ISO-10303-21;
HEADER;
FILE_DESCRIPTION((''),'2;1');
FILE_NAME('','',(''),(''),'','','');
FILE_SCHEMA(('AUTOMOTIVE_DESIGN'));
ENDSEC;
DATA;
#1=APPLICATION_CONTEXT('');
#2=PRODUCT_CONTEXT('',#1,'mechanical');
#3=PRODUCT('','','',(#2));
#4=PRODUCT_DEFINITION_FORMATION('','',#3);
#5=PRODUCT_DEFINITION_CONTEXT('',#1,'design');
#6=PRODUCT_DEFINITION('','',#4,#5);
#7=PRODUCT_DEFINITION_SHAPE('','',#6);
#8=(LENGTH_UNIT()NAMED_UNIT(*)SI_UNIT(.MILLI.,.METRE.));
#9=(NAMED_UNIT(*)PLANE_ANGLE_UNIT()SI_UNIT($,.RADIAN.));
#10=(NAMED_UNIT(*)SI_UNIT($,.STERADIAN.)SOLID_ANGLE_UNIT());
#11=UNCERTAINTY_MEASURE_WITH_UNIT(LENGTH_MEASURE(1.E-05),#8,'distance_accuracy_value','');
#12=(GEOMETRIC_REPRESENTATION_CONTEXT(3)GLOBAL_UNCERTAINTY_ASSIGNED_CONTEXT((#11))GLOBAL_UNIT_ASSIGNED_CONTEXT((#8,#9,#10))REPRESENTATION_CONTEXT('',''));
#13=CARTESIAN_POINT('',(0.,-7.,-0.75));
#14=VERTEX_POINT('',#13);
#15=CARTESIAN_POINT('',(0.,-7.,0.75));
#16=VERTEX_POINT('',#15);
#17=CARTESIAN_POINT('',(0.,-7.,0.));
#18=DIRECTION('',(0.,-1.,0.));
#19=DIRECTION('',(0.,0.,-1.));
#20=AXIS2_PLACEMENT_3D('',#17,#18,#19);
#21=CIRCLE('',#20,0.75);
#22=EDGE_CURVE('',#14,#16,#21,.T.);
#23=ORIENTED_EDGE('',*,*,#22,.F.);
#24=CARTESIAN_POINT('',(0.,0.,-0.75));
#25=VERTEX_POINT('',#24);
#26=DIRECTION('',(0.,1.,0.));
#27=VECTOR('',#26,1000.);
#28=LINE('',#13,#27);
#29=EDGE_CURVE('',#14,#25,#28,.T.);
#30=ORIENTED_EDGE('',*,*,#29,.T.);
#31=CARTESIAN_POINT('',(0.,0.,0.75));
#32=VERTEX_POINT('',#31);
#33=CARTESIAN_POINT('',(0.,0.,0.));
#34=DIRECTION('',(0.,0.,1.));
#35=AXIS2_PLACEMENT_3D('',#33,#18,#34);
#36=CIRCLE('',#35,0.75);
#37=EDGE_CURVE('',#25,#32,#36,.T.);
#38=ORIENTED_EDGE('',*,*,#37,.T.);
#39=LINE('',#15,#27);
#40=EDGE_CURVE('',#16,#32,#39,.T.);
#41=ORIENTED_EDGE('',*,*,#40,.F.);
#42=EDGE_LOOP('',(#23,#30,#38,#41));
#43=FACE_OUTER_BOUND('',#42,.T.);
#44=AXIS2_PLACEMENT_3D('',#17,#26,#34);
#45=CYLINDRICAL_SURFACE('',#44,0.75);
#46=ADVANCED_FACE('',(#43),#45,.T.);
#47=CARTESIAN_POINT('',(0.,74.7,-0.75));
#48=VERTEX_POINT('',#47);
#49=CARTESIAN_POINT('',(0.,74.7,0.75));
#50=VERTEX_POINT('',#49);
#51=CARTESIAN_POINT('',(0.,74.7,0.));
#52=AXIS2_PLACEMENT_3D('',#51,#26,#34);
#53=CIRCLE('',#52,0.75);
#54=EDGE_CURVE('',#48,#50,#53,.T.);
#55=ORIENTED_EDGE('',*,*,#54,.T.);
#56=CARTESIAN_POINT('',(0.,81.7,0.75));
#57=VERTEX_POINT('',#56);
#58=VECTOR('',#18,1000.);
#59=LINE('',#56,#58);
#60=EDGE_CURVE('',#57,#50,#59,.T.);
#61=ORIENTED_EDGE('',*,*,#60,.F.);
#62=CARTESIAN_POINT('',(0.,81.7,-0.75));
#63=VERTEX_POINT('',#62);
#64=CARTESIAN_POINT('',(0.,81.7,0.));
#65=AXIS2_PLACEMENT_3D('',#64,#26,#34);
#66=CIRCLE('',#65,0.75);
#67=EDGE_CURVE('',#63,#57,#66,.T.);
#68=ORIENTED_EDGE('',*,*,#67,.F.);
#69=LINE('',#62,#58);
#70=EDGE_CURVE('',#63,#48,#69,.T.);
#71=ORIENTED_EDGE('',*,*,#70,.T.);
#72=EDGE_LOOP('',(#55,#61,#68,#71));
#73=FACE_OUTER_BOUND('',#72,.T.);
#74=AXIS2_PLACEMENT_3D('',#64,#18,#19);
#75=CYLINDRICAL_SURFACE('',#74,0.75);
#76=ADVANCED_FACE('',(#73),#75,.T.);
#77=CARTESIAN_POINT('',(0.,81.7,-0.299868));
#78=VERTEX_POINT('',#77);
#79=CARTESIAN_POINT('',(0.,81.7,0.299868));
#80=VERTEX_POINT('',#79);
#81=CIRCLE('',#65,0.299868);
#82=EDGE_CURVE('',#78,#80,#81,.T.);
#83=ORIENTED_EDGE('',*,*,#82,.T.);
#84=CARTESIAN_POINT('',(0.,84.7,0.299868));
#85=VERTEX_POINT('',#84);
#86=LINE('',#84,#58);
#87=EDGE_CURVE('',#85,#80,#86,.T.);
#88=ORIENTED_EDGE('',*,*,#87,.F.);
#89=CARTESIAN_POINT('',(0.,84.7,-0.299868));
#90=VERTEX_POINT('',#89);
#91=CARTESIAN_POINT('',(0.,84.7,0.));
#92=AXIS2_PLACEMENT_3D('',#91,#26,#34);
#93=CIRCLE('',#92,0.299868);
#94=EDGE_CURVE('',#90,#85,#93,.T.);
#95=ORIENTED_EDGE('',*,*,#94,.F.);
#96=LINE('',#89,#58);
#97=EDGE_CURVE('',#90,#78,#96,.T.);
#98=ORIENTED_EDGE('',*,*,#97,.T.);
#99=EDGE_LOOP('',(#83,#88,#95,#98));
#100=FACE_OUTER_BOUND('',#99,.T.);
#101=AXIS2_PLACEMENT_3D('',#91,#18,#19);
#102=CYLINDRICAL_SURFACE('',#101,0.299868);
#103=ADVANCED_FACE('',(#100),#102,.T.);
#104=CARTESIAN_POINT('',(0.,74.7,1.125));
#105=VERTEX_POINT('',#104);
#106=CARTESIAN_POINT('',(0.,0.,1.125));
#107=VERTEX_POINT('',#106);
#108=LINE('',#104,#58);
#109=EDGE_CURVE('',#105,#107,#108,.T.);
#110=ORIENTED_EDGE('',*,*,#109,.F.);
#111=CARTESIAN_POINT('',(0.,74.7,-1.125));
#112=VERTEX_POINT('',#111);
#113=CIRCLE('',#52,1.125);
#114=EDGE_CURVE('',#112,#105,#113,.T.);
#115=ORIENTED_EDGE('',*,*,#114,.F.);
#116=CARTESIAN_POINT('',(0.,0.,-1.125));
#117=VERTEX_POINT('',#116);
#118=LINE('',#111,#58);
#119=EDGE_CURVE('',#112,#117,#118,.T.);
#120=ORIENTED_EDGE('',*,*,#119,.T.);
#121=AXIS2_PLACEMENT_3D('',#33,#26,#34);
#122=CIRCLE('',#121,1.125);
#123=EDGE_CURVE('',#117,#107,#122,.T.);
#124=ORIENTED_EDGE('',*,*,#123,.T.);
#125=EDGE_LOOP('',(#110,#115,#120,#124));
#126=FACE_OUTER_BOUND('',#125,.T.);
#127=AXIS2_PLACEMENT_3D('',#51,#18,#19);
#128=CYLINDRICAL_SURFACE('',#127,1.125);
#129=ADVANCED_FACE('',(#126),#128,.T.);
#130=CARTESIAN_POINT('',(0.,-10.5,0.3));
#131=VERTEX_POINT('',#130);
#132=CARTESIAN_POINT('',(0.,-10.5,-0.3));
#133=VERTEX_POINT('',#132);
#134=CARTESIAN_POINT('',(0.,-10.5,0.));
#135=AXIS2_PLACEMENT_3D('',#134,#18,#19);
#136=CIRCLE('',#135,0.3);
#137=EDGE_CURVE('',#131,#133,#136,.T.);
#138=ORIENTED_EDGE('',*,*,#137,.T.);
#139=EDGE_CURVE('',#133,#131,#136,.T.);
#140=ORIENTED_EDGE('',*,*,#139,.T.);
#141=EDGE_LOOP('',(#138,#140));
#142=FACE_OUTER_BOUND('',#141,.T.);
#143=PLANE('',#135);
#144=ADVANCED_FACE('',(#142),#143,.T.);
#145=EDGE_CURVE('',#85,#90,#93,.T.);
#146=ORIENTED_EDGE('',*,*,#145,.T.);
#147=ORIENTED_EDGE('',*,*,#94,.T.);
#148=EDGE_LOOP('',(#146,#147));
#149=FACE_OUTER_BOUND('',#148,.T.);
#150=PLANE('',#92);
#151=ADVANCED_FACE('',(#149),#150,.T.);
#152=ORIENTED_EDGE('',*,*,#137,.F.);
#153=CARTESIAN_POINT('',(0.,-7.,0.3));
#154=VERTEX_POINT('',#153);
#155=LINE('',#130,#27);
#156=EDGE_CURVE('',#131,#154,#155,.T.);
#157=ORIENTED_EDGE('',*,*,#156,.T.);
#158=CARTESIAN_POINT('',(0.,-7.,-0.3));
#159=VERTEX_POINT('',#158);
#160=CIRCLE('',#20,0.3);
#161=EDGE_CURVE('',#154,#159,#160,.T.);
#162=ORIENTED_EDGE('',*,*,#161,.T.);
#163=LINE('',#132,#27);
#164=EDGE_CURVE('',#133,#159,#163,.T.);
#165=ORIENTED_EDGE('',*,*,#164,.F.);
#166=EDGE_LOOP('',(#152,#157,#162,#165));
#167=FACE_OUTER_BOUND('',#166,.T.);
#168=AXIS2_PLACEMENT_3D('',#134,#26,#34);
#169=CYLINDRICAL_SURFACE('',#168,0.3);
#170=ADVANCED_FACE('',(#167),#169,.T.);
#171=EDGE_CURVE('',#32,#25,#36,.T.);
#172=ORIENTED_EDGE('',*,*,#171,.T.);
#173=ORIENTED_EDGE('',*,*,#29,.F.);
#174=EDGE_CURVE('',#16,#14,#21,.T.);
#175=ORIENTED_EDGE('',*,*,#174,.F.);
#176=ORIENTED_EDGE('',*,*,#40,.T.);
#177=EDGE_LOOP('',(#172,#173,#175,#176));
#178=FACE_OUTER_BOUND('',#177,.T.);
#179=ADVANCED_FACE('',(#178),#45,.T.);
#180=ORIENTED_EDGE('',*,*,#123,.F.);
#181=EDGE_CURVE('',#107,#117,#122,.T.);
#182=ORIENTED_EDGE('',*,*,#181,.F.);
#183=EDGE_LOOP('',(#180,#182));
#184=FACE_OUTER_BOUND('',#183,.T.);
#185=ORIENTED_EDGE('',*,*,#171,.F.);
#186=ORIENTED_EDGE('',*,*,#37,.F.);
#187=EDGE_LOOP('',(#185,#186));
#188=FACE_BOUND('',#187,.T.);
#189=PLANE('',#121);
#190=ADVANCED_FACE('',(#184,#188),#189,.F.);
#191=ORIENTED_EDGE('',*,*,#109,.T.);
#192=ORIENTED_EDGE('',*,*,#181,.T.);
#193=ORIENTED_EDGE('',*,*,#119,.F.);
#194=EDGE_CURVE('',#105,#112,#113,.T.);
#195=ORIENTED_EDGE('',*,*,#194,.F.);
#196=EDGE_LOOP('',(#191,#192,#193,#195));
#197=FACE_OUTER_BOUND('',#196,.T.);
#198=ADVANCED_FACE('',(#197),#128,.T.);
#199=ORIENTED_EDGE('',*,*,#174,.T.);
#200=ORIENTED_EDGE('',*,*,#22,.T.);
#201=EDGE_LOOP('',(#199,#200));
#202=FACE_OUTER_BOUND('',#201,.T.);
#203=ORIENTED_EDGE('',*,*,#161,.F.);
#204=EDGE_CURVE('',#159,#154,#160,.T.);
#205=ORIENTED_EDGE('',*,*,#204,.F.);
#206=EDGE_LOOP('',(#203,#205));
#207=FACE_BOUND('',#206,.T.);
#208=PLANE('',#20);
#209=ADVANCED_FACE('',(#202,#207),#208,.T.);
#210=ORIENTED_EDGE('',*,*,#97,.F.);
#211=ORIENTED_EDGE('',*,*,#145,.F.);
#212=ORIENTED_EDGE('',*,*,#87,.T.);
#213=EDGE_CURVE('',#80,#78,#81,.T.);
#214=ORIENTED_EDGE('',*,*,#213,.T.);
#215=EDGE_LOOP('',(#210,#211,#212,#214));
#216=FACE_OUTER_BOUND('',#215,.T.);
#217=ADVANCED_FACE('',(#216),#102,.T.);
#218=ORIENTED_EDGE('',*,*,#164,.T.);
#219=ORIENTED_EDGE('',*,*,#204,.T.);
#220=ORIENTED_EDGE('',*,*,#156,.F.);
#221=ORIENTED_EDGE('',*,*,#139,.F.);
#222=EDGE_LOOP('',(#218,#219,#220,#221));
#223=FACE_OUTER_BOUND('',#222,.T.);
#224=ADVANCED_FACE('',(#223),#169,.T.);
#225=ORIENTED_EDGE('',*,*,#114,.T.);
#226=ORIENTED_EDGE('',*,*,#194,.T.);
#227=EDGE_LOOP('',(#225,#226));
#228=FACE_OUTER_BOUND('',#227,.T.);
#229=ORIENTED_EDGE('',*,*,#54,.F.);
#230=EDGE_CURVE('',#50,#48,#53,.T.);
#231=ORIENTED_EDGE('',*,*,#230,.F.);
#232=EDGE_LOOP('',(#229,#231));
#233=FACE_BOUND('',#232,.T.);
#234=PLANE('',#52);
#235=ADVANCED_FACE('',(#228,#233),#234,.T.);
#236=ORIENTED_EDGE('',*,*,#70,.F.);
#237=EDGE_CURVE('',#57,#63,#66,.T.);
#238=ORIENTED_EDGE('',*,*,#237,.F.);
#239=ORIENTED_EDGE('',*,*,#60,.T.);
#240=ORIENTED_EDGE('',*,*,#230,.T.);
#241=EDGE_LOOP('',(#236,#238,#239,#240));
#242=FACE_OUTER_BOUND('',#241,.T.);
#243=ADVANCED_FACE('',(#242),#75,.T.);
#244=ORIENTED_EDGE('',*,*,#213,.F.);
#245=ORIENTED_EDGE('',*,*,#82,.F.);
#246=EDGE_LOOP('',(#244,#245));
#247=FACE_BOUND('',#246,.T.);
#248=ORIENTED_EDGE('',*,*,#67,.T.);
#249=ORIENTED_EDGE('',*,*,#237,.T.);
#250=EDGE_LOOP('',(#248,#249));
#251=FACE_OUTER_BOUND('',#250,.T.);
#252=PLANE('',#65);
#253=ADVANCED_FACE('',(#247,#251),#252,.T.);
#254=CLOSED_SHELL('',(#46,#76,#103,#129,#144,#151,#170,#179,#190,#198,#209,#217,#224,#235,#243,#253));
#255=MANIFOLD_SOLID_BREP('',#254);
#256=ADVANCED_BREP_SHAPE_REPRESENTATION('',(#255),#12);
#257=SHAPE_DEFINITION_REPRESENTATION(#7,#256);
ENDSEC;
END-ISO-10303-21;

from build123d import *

# Parameters (mm, degrees)
SKETCH1_R           = 1.125
BOSS_EXTRUDE1_DEPTH = 74.7
SKETCH2_R           = 0.75
BOSS_EXTRUDE2_DEPTH = 7
SKETCH3_R           = 0.3
BOSS_EXTRUDE3_DEPTH = 3.5
BOSS_EXTRUDE4_START = 7
SKETCH4_R           = 0.75
BOSS_EXTRUDE4_DEPTH = 7
SKETCH5_R           = 0.299867591
BOSS_EXTRUDE5_DEPTH = 3


with BuildPart() as part:
    # Sketch1 → Boss-Extrude1 (new body)
    with BuildSketch(Plane(origin=(0, 0, 0), x_dir=(1, 0, 0), z_dir=(0, 1, 0))):
        with Locations(Location((0, 0, 0), (0, 0, 270))):
            Circle(SKETCH1_R)
    extrude(amount=BOSS_EXTRUDE1_DEPTH)

    # Sketch2 → Boss-Extrude2 (add)
    with BuildSketch(Plane.XZ):
        with Locations(Location((0, 0, 0), (0, 0, 90))):
            Circle(SKETCH2_R)
    extrude(amount=BOSS_EXTRUDE2_DEPTH)

    # Sketch3 → Boss-Extrude3 (add)
    with BuildSketch(Plane.XZ.offset(7)):
        with Locations(Location((0, 0, 0), (0, 0, 270))):
            Circle(SKETCH3_R)
    extrude(amount=BOSS_EXTRUDE3_DEPTH)

    # Sketch4 → Boss-Extrude4 (add)
    with BuildSketch(Plane(origin=(0, 74.7, 0), x_dir=(1, 0, 0), z_dir=(0, 1, 0)).offset(BOSS_EXTRUDE4_START)):
        with Locations(Location((0, 0, 0), (0, 0, 270))):
            Circle(SKETCH4_R)
    extrude(amount=-BOSS_EXTRUDE4_DEPTH)

    # Sketch5 → Boss-Extrude5 (add)
    with BuildSketch(Plane(origin=(0, 81.7, 0), x_dir=(1, 0, 0), z_dir=(0, 1, 0))):
        with Locations(Location((0, 0, 0), (0, 0, 270))):
            Circle(SKETCH5_R)
    extrude(amount=BOSS_EXTRUDE5_DEPTH)


solid = part.part
